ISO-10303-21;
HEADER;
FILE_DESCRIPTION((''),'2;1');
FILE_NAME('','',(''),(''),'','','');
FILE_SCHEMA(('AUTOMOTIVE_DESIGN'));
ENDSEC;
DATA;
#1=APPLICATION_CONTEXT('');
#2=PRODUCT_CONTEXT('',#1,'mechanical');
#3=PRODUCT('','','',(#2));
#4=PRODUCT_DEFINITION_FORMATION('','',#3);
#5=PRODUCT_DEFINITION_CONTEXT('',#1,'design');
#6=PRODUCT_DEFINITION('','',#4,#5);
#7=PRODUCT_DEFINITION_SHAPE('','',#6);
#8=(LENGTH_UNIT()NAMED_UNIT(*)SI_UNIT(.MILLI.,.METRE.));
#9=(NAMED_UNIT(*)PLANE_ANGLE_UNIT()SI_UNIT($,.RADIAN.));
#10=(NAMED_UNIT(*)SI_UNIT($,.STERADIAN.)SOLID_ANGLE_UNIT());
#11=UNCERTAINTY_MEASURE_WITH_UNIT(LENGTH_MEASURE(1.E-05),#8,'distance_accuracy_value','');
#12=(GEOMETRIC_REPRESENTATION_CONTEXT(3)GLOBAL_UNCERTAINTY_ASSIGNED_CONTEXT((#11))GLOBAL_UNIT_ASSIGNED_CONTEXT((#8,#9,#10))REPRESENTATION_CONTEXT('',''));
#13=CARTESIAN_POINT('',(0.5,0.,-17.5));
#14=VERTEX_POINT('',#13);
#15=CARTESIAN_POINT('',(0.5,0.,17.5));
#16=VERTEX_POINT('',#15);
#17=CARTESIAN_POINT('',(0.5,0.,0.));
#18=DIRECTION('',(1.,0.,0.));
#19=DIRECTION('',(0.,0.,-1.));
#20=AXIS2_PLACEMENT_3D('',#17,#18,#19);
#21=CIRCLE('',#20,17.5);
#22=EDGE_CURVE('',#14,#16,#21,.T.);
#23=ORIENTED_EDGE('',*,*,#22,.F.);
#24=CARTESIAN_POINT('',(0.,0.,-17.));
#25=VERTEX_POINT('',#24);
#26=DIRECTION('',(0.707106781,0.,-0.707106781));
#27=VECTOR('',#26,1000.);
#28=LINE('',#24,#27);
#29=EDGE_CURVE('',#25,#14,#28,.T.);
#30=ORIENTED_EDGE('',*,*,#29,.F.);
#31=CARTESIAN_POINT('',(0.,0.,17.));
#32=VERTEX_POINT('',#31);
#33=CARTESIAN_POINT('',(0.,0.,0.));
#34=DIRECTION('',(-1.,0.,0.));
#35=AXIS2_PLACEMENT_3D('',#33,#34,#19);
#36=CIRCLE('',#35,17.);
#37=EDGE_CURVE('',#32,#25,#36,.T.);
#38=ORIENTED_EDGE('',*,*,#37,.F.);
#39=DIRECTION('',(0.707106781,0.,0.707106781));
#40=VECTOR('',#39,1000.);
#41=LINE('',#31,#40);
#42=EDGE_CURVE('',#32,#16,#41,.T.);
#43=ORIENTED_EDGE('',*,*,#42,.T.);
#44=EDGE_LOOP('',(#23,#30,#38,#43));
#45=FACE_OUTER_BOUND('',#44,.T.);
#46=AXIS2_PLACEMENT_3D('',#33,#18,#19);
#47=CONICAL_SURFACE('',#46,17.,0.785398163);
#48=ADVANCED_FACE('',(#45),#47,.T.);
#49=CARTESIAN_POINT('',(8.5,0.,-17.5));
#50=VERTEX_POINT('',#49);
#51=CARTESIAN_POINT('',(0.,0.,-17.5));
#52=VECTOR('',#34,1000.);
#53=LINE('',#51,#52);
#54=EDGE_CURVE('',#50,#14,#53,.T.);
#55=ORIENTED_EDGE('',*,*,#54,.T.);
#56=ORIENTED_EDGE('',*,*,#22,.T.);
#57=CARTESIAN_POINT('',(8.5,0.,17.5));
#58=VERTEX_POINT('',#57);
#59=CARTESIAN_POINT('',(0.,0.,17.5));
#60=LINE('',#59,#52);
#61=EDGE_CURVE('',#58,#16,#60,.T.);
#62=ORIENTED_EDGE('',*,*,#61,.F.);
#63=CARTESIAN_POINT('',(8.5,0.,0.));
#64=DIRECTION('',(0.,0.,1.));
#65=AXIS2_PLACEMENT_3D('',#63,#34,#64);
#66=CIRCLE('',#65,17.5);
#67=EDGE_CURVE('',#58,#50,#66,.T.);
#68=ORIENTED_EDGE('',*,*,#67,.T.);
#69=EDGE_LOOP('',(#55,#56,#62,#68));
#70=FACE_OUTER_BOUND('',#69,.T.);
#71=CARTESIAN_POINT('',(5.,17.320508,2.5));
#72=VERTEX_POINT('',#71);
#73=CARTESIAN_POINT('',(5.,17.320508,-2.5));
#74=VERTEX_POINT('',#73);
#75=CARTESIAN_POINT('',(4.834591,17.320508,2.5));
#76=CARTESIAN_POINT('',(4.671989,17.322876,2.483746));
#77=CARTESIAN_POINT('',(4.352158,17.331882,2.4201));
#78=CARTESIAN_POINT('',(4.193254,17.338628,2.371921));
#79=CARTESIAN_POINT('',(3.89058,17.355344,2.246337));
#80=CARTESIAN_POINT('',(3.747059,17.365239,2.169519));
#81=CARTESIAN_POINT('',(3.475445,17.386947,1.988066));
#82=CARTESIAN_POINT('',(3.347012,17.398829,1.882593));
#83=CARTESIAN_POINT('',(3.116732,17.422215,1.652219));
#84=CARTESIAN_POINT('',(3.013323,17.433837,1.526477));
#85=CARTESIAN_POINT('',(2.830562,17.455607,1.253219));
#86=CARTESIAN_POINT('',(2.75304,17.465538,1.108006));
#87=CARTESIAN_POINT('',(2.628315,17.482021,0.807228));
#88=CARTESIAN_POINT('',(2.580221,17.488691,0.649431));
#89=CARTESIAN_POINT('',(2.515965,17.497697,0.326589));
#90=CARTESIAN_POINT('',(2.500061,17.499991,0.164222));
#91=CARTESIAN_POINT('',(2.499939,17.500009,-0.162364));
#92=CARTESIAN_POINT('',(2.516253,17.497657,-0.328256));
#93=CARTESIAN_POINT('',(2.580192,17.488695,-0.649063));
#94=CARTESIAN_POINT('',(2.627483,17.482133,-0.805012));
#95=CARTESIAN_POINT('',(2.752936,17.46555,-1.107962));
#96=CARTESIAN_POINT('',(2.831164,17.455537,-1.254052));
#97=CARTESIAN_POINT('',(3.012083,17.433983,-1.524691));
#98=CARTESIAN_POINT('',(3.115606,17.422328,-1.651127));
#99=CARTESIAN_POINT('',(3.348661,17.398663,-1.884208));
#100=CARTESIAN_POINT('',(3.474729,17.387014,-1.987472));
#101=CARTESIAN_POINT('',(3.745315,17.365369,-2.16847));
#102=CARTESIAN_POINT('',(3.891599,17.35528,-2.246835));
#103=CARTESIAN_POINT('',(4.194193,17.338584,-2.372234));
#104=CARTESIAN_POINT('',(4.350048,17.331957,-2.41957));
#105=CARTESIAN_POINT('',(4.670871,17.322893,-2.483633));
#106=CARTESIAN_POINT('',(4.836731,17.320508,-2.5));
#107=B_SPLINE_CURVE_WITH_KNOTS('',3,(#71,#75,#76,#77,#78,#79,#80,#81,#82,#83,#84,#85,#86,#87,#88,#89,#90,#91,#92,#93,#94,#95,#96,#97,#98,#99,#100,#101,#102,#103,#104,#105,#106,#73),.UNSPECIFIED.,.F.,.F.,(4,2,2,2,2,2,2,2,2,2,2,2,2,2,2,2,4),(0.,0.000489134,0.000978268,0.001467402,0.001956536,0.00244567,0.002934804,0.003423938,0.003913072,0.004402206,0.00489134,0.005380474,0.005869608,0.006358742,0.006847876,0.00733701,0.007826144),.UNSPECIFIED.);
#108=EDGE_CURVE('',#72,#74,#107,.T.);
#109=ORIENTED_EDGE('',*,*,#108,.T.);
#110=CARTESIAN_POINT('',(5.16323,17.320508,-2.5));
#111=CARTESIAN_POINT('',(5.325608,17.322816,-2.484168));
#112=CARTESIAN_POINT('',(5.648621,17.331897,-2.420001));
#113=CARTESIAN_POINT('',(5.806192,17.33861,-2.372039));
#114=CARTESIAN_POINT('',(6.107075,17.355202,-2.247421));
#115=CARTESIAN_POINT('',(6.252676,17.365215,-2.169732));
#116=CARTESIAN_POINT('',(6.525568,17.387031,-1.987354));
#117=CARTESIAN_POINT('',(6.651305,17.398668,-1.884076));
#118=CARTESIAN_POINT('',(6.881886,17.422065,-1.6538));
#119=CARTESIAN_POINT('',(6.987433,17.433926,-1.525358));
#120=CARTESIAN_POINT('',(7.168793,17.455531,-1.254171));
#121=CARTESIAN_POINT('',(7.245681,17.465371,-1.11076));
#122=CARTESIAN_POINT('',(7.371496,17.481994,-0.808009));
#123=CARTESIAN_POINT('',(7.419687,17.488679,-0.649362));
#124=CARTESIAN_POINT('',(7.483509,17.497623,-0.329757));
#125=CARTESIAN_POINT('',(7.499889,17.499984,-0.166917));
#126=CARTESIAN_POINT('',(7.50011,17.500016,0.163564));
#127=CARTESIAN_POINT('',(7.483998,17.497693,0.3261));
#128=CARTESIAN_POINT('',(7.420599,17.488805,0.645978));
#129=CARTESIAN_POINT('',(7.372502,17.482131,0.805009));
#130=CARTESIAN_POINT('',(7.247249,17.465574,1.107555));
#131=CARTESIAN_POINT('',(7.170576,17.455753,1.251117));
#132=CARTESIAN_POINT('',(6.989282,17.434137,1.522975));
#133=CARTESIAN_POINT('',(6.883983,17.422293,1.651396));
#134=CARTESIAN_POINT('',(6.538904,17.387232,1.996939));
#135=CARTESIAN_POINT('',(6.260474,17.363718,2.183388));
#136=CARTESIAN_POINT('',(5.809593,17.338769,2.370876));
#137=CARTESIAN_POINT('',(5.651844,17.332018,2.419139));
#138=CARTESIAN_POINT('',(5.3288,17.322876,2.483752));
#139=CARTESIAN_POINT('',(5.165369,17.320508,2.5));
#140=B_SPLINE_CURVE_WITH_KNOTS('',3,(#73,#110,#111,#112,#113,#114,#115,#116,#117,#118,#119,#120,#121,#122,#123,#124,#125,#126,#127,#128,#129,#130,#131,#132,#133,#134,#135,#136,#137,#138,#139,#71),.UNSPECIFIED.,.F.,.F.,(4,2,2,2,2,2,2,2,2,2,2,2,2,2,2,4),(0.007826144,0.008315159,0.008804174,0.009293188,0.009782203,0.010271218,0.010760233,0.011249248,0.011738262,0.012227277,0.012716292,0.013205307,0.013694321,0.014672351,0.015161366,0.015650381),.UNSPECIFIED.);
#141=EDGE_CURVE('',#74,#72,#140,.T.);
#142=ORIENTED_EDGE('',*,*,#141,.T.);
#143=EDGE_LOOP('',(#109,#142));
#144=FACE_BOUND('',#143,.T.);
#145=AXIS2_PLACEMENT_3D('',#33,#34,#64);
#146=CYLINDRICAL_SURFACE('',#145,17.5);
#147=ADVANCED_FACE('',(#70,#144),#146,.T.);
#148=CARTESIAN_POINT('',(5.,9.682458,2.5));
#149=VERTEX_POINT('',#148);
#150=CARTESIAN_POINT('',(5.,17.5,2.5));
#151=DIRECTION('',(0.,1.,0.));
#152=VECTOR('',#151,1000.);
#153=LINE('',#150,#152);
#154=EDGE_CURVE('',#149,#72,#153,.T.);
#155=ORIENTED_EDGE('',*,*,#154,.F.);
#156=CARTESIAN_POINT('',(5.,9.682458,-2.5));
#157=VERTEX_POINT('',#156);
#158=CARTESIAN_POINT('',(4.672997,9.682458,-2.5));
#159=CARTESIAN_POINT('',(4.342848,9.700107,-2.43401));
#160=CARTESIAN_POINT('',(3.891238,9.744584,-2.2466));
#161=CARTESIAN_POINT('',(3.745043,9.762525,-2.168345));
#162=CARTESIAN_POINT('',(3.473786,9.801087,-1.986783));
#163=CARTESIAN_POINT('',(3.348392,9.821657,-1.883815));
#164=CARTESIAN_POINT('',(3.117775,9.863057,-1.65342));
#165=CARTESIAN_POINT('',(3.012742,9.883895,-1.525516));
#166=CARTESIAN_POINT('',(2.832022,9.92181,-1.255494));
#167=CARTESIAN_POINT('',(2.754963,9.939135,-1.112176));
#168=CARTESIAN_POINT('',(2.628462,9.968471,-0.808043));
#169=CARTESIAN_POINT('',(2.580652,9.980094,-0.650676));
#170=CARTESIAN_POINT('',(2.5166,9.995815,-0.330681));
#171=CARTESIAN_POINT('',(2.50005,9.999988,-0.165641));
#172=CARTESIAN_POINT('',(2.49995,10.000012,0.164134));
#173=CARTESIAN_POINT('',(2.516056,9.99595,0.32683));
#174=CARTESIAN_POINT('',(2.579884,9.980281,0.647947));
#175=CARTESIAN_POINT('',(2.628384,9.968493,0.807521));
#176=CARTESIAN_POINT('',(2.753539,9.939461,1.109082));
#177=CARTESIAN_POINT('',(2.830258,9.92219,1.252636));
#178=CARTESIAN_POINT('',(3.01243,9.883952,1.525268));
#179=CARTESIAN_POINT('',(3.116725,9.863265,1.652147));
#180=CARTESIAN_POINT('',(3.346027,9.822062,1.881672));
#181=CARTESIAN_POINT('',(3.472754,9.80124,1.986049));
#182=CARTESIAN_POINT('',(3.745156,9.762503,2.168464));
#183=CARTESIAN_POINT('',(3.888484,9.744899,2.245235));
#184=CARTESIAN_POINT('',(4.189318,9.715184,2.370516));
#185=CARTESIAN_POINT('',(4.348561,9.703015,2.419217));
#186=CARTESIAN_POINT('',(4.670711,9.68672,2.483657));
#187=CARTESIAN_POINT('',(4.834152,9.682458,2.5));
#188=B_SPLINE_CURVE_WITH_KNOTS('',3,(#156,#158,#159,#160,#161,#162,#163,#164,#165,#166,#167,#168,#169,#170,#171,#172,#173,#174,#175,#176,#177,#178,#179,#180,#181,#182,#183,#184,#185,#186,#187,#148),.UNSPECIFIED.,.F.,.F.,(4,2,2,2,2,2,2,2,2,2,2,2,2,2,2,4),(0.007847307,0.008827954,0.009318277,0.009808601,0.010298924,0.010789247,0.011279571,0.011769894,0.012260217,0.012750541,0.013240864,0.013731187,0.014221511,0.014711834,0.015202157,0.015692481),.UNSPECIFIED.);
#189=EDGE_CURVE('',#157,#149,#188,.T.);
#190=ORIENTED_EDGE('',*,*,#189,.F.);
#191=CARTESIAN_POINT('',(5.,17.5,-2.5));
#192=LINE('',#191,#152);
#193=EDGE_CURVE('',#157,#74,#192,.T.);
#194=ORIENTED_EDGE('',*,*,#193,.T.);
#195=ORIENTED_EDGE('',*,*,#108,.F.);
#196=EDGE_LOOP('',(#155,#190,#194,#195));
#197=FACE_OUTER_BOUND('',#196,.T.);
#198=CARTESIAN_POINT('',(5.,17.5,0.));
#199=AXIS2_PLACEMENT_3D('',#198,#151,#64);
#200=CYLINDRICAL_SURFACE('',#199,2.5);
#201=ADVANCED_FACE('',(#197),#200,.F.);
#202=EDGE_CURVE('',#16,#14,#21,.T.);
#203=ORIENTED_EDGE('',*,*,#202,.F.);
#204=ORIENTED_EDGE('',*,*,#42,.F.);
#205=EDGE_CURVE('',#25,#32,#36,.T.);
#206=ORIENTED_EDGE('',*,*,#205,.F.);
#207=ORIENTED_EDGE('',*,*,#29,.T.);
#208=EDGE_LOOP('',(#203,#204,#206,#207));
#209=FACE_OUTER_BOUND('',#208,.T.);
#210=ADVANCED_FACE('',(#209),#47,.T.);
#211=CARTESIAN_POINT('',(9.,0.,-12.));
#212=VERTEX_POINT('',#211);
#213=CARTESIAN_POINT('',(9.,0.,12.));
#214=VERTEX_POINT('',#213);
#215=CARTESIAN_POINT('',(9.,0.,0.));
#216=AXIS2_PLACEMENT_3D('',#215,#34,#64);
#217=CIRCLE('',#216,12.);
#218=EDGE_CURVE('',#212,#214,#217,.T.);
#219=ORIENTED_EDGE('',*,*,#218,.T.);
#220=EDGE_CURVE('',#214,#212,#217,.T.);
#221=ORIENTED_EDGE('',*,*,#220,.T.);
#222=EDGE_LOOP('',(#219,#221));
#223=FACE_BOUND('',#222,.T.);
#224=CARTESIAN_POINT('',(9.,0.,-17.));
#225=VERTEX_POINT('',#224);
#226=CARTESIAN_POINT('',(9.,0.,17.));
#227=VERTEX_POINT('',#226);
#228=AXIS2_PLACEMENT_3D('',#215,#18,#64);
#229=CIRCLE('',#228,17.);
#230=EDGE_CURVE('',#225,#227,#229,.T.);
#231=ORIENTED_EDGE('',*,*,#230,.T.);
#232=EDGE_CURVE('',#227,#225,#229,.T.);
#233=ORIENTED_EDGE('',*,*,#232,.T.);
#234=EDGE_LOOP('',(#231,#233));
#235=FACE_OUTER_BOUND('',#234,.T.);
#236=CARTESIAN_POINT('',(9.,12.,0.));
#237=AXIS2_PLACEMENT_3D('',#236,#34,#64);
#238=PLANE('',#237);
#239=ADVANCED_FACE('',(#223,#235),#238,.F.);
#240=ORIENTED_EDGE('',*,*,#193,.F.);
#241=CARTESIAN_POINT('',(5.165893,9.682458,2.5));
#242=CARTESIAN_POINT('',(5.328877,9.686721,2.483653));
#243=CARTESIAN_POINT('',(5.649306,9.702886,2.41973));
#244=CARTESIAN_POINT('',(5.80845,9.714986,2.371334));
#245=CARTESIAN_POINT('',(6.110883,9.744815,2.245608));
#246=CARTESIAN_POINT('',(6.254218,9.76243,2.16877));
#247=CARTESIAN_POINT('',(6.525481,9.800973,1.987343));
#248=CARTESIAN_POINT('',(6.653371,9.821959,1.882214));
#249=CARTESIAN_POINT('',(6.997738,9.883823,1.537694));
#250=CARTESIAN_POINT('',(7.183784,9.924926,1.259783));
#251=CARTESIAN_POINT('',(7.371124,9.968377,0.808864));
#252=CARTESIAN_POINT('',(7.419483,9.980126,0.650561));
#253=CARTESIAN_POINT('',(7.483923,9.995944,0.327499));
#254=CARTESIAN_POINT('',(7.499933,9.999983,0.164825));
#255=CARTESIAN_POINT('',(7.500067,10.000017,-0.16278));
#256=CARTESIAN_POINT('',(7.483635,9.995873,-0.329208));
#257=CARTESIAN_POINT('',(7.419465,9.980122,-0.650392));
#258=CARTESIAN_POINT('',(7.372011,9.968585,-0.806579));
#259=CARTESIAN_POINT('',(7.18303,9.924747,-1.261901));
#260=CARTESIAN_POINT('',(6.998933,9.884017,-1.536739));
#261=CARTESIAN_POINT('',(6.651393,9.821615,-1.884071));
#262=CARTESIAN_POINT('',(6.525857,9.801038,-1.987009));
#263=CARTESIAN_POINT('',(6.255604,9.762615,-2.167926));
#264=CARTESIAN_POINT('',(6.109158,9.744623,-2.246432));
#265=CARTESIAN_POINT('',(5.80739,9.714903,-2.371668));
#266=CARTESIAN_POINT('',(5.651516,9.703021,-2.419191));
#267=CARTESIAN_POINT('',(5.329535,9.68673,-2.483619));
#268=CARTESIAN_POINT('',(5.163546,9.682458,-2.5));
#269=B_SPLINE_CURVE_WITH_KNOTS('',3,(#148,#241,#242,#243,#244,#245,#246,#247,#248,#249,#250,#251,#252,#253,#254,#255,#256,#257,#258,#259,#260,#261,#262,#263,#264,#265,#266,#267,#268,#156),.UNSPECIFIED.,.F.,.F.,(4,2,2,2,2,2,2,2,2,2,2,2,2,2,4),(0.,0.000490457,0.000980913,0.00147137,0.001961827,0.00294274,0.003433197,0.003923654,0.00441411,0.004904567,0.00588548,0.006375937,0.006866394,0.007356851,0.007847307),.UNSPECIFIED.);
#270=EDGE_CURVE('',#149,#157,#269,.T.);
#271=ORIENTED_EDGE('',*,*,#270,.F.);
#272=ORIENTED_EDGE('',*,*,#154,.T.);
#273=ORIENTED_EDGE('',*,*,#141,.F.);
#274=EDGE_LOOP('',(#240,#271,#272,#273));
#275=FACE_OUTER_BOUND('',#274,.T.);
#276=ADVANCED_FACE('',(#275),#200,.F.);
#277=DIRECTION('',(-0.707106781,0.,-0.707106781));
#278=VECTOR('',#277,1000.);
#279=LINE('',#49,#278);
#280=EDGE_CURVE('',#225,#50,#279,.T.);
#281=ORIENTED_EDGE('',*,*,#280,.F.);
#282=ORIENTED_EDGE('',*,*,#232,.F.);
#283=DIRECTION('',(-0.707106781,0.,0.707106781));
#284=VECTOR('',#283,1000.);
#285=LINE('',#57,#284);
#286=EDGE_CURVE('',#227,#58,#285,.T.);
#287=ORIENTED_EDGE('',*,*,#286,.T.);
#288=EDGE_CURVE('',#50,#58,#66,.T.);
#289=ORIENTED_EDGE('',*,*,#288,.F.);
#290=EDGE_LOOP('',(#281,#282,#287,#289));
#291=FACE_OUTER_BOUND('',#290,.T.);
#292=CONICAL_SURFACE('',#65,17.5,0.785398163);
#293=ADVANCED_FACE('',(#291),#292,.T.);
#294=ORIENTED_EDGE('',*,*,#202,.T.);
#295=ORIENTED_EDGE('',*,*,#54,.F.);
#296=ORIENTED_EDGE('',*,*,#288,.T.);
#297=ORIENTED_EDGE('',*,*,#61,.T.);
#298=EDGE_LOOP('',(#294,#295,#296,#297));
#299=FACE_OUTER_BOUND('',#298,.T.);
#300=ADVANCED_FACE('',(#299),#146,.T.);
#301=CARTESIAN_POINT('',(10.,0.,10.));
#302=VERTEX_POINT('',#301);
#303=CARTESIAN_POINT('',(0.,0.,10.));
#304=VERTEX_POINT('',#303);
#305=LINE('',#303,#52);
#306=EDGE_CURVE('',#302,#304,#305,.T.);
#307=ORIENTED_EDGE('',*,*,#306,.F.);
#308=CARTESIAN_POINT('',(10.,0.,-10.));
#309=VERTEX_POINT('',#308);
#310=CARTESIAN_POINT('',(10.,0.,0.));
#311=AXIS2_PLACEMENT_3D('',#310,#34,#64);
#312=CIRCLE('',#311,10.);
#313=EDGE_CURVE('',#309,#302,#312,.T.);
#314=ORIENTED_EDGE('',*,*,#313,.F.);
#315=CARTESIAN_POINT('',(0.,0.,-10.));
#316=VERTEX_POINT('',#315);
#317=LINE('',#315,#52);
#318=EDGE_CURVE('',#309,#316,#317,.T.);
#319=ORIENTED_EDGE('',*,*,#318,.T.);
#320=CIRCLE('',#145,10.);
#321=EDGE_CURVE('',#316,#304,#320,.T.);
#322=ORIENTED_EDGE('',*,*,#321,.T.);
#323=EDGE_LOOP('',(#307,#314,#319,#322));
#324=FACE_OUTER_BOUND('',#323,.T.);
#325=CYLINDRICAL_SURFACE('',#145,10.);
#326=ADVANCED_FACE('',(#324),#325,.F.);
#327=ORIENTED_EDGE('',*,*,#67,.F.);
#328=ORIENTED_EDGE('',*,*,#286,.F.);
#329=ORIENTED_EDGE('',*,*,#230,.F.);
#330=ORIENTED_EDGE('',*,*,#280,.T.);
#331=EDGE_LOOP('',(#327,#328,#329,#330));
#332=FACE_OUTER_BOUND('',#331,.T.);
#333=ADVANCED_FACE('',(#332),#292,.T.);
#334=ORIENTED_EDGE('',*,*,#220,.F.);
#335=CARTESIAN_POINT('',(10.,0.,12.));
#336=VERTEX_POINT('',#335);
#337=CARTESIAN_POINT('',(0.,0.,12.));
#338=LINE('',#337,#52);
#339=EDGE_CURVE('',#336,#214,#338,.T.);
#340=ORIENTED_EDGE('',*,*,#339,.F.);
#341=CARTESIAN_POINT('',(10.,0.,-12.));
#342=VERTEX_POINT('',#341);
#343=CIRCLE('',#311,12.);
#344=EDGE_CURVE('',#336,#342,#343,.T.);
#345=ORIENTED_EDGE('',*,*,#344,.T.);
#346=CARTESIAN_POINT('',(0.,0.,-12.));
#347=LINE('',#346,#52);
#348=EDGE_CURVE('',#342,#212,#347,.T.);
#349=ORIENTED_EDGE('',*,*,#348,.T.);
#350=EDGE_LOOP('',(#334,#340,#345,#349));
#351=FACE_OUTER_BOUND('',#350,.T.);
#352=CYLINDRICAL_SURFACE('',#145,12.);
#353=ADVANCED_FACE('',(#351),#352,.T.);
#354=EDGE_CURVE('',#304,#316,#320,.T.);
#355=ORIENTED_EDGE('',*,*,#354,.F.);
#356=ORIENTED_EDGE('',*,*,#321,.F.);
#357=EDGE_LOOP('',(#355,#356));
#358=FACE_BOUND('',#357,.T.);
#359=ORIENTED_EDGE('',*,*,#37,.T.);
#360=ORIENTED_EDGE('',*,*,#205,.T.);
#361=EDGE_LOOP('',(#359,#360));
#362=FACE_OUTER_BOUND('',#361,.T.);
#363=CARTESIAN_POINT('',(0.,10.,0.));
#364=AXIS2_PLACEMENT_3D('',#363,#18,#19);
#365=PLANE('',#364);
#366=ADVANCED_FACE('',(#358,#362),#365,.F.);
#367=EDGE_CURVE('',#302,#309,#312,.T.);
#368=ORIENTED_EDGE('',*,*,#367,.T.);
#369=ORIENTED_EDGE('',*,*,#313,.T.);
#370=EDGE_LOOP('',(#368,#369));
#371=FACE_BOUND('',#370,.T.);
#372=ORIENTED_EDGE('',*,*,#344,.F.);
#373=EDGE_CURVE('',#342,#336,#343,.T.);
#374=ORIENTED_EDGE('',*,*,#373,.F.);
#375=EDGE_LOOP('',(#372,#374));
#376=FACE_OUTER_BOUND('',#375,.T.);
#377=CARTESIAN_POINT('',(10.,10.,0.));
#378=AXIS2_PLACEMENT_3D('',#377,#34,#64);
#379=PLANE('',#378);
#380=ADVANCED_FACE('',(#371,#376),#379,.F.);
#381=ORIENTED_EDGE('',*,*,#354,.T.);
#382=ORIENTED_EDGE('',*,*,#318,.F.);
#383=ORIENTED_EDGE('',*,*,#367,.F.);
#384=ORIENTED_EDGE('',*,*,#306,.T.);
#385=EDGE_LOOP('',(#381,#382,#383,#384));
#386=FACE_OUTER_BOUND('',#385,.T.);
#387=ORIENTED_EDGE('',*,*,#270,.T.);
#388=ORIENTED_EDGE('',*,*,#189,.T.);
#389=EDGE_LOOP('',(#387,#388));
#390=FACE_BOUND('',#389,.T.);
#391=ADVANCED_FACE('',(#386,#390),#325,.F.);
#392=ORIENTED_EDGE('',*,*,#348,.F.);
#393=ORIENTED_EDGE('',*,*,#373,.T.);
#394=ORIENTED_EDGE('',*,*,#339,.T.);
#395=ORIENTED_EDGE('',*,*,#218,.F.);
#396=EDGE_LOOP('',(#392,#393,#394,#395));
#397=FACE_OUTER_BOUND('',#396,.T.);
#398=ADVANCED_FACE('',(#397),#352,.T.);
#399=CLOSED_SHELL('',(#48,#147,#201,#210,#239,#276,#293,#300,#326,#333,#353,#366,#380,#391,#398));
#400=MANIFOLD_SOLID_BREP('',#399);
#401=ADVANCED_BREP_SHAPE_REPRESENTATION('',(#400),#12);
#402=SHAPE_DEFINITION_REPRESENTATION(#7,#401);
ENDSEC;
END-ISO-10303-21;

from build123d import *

# Parameters (mm, degrees)
M6_TAPPED_HOLE1_D               = 5
M6_TAPPED_HOLE1_DEPTH           = 15
M6_TAPPED_HOLE1_TIP             = 1.502151548
M6_TAPPED_HOLE1_ON_FACE_2_D     = 5
M6_TAPPED_HOLE1_ON_FACE_2_DEPTH = 15
M6_TAPPED_HOLE1_ON_FACE_2_TIP   = 1.502151548
CHAMFER1_SIZE                   = 0.5


with BuildPart() as part:
    # Sketch1 → Revolve1 (revolve)
    with BuildSketch(Plane.XY, mode=Mode.PRIVATE) as revolve1_sk:
        Polygon((0, 10), (10, 10), (10, 12), (9, 12), (9, 17.5), (0, 17.5), align=None)
    revolve(revolve1_sk.sketch.rotate(Axis((0, 0, 0), (1, 0, 0)), 90), axis=Axis((0, 0, 0), (1, 0, 0)))

    # M6 Tapped Hole1
    with Locations(Plane(origin=(5, 17.5, 0), x_dir=(0, 0, 1), z_dir=(0, 1, 0))):
        with Locations((0, 0)):
            Hole(M6_TAPPED_HOLE1_D / 2, depth=M6_TAPPED_HOLE1_DEPTH)
            with Locations((0, 0, -(M6_TAPPED_HOLE1_DEPTH + M6_TAPPED_HOLE1_TIP / 2))):  # 118° drill point
                Cone(0, M6_TAPPED_HOLE1_D / 2, M6_TAPPED_HOLE1_TIP, mode=Mode.SUBTRACT)

    # M6 Tapped Hole1 on face 2
    with Locations(Plane(origin=(-19.39268328, -13.895465991, 0), x_dir=(0, 0, 1), z_dir=(0, 1, 0))):
        with Locations((0, 0)):
            Hole(M6_TAPPED_HOLE1_ON_FACE_2_D / 2, depth=M6_TAPPED_HOLE1_ON_FACE_2_DEPTH)
            with Locations((0, 0, -(M6_TAPPED_HOLE1_ON_FACE_2_DEPTH + M6_TAPPED_HOLE1_ON_FACE_2_TIP / 2))):  # 118° drill point
                Cone(0, M6_TAPPED_HOLE1_ON_FACE_2_D / 2, M6_TAPPED_HOLE1_ON_FACE_2_TIP, mode=Mode.SUBTRACT)

    # Chamfer1
    chamfer1_edges = [part.edges().sort_by_distance(p)[0] for p in [
        (9, 0, -17.5),
        (0, 0, -17.5),
    ]]
    chamfer(chamfer1_edges, length=CHAMFER1_SIZE)


solid = part.part
